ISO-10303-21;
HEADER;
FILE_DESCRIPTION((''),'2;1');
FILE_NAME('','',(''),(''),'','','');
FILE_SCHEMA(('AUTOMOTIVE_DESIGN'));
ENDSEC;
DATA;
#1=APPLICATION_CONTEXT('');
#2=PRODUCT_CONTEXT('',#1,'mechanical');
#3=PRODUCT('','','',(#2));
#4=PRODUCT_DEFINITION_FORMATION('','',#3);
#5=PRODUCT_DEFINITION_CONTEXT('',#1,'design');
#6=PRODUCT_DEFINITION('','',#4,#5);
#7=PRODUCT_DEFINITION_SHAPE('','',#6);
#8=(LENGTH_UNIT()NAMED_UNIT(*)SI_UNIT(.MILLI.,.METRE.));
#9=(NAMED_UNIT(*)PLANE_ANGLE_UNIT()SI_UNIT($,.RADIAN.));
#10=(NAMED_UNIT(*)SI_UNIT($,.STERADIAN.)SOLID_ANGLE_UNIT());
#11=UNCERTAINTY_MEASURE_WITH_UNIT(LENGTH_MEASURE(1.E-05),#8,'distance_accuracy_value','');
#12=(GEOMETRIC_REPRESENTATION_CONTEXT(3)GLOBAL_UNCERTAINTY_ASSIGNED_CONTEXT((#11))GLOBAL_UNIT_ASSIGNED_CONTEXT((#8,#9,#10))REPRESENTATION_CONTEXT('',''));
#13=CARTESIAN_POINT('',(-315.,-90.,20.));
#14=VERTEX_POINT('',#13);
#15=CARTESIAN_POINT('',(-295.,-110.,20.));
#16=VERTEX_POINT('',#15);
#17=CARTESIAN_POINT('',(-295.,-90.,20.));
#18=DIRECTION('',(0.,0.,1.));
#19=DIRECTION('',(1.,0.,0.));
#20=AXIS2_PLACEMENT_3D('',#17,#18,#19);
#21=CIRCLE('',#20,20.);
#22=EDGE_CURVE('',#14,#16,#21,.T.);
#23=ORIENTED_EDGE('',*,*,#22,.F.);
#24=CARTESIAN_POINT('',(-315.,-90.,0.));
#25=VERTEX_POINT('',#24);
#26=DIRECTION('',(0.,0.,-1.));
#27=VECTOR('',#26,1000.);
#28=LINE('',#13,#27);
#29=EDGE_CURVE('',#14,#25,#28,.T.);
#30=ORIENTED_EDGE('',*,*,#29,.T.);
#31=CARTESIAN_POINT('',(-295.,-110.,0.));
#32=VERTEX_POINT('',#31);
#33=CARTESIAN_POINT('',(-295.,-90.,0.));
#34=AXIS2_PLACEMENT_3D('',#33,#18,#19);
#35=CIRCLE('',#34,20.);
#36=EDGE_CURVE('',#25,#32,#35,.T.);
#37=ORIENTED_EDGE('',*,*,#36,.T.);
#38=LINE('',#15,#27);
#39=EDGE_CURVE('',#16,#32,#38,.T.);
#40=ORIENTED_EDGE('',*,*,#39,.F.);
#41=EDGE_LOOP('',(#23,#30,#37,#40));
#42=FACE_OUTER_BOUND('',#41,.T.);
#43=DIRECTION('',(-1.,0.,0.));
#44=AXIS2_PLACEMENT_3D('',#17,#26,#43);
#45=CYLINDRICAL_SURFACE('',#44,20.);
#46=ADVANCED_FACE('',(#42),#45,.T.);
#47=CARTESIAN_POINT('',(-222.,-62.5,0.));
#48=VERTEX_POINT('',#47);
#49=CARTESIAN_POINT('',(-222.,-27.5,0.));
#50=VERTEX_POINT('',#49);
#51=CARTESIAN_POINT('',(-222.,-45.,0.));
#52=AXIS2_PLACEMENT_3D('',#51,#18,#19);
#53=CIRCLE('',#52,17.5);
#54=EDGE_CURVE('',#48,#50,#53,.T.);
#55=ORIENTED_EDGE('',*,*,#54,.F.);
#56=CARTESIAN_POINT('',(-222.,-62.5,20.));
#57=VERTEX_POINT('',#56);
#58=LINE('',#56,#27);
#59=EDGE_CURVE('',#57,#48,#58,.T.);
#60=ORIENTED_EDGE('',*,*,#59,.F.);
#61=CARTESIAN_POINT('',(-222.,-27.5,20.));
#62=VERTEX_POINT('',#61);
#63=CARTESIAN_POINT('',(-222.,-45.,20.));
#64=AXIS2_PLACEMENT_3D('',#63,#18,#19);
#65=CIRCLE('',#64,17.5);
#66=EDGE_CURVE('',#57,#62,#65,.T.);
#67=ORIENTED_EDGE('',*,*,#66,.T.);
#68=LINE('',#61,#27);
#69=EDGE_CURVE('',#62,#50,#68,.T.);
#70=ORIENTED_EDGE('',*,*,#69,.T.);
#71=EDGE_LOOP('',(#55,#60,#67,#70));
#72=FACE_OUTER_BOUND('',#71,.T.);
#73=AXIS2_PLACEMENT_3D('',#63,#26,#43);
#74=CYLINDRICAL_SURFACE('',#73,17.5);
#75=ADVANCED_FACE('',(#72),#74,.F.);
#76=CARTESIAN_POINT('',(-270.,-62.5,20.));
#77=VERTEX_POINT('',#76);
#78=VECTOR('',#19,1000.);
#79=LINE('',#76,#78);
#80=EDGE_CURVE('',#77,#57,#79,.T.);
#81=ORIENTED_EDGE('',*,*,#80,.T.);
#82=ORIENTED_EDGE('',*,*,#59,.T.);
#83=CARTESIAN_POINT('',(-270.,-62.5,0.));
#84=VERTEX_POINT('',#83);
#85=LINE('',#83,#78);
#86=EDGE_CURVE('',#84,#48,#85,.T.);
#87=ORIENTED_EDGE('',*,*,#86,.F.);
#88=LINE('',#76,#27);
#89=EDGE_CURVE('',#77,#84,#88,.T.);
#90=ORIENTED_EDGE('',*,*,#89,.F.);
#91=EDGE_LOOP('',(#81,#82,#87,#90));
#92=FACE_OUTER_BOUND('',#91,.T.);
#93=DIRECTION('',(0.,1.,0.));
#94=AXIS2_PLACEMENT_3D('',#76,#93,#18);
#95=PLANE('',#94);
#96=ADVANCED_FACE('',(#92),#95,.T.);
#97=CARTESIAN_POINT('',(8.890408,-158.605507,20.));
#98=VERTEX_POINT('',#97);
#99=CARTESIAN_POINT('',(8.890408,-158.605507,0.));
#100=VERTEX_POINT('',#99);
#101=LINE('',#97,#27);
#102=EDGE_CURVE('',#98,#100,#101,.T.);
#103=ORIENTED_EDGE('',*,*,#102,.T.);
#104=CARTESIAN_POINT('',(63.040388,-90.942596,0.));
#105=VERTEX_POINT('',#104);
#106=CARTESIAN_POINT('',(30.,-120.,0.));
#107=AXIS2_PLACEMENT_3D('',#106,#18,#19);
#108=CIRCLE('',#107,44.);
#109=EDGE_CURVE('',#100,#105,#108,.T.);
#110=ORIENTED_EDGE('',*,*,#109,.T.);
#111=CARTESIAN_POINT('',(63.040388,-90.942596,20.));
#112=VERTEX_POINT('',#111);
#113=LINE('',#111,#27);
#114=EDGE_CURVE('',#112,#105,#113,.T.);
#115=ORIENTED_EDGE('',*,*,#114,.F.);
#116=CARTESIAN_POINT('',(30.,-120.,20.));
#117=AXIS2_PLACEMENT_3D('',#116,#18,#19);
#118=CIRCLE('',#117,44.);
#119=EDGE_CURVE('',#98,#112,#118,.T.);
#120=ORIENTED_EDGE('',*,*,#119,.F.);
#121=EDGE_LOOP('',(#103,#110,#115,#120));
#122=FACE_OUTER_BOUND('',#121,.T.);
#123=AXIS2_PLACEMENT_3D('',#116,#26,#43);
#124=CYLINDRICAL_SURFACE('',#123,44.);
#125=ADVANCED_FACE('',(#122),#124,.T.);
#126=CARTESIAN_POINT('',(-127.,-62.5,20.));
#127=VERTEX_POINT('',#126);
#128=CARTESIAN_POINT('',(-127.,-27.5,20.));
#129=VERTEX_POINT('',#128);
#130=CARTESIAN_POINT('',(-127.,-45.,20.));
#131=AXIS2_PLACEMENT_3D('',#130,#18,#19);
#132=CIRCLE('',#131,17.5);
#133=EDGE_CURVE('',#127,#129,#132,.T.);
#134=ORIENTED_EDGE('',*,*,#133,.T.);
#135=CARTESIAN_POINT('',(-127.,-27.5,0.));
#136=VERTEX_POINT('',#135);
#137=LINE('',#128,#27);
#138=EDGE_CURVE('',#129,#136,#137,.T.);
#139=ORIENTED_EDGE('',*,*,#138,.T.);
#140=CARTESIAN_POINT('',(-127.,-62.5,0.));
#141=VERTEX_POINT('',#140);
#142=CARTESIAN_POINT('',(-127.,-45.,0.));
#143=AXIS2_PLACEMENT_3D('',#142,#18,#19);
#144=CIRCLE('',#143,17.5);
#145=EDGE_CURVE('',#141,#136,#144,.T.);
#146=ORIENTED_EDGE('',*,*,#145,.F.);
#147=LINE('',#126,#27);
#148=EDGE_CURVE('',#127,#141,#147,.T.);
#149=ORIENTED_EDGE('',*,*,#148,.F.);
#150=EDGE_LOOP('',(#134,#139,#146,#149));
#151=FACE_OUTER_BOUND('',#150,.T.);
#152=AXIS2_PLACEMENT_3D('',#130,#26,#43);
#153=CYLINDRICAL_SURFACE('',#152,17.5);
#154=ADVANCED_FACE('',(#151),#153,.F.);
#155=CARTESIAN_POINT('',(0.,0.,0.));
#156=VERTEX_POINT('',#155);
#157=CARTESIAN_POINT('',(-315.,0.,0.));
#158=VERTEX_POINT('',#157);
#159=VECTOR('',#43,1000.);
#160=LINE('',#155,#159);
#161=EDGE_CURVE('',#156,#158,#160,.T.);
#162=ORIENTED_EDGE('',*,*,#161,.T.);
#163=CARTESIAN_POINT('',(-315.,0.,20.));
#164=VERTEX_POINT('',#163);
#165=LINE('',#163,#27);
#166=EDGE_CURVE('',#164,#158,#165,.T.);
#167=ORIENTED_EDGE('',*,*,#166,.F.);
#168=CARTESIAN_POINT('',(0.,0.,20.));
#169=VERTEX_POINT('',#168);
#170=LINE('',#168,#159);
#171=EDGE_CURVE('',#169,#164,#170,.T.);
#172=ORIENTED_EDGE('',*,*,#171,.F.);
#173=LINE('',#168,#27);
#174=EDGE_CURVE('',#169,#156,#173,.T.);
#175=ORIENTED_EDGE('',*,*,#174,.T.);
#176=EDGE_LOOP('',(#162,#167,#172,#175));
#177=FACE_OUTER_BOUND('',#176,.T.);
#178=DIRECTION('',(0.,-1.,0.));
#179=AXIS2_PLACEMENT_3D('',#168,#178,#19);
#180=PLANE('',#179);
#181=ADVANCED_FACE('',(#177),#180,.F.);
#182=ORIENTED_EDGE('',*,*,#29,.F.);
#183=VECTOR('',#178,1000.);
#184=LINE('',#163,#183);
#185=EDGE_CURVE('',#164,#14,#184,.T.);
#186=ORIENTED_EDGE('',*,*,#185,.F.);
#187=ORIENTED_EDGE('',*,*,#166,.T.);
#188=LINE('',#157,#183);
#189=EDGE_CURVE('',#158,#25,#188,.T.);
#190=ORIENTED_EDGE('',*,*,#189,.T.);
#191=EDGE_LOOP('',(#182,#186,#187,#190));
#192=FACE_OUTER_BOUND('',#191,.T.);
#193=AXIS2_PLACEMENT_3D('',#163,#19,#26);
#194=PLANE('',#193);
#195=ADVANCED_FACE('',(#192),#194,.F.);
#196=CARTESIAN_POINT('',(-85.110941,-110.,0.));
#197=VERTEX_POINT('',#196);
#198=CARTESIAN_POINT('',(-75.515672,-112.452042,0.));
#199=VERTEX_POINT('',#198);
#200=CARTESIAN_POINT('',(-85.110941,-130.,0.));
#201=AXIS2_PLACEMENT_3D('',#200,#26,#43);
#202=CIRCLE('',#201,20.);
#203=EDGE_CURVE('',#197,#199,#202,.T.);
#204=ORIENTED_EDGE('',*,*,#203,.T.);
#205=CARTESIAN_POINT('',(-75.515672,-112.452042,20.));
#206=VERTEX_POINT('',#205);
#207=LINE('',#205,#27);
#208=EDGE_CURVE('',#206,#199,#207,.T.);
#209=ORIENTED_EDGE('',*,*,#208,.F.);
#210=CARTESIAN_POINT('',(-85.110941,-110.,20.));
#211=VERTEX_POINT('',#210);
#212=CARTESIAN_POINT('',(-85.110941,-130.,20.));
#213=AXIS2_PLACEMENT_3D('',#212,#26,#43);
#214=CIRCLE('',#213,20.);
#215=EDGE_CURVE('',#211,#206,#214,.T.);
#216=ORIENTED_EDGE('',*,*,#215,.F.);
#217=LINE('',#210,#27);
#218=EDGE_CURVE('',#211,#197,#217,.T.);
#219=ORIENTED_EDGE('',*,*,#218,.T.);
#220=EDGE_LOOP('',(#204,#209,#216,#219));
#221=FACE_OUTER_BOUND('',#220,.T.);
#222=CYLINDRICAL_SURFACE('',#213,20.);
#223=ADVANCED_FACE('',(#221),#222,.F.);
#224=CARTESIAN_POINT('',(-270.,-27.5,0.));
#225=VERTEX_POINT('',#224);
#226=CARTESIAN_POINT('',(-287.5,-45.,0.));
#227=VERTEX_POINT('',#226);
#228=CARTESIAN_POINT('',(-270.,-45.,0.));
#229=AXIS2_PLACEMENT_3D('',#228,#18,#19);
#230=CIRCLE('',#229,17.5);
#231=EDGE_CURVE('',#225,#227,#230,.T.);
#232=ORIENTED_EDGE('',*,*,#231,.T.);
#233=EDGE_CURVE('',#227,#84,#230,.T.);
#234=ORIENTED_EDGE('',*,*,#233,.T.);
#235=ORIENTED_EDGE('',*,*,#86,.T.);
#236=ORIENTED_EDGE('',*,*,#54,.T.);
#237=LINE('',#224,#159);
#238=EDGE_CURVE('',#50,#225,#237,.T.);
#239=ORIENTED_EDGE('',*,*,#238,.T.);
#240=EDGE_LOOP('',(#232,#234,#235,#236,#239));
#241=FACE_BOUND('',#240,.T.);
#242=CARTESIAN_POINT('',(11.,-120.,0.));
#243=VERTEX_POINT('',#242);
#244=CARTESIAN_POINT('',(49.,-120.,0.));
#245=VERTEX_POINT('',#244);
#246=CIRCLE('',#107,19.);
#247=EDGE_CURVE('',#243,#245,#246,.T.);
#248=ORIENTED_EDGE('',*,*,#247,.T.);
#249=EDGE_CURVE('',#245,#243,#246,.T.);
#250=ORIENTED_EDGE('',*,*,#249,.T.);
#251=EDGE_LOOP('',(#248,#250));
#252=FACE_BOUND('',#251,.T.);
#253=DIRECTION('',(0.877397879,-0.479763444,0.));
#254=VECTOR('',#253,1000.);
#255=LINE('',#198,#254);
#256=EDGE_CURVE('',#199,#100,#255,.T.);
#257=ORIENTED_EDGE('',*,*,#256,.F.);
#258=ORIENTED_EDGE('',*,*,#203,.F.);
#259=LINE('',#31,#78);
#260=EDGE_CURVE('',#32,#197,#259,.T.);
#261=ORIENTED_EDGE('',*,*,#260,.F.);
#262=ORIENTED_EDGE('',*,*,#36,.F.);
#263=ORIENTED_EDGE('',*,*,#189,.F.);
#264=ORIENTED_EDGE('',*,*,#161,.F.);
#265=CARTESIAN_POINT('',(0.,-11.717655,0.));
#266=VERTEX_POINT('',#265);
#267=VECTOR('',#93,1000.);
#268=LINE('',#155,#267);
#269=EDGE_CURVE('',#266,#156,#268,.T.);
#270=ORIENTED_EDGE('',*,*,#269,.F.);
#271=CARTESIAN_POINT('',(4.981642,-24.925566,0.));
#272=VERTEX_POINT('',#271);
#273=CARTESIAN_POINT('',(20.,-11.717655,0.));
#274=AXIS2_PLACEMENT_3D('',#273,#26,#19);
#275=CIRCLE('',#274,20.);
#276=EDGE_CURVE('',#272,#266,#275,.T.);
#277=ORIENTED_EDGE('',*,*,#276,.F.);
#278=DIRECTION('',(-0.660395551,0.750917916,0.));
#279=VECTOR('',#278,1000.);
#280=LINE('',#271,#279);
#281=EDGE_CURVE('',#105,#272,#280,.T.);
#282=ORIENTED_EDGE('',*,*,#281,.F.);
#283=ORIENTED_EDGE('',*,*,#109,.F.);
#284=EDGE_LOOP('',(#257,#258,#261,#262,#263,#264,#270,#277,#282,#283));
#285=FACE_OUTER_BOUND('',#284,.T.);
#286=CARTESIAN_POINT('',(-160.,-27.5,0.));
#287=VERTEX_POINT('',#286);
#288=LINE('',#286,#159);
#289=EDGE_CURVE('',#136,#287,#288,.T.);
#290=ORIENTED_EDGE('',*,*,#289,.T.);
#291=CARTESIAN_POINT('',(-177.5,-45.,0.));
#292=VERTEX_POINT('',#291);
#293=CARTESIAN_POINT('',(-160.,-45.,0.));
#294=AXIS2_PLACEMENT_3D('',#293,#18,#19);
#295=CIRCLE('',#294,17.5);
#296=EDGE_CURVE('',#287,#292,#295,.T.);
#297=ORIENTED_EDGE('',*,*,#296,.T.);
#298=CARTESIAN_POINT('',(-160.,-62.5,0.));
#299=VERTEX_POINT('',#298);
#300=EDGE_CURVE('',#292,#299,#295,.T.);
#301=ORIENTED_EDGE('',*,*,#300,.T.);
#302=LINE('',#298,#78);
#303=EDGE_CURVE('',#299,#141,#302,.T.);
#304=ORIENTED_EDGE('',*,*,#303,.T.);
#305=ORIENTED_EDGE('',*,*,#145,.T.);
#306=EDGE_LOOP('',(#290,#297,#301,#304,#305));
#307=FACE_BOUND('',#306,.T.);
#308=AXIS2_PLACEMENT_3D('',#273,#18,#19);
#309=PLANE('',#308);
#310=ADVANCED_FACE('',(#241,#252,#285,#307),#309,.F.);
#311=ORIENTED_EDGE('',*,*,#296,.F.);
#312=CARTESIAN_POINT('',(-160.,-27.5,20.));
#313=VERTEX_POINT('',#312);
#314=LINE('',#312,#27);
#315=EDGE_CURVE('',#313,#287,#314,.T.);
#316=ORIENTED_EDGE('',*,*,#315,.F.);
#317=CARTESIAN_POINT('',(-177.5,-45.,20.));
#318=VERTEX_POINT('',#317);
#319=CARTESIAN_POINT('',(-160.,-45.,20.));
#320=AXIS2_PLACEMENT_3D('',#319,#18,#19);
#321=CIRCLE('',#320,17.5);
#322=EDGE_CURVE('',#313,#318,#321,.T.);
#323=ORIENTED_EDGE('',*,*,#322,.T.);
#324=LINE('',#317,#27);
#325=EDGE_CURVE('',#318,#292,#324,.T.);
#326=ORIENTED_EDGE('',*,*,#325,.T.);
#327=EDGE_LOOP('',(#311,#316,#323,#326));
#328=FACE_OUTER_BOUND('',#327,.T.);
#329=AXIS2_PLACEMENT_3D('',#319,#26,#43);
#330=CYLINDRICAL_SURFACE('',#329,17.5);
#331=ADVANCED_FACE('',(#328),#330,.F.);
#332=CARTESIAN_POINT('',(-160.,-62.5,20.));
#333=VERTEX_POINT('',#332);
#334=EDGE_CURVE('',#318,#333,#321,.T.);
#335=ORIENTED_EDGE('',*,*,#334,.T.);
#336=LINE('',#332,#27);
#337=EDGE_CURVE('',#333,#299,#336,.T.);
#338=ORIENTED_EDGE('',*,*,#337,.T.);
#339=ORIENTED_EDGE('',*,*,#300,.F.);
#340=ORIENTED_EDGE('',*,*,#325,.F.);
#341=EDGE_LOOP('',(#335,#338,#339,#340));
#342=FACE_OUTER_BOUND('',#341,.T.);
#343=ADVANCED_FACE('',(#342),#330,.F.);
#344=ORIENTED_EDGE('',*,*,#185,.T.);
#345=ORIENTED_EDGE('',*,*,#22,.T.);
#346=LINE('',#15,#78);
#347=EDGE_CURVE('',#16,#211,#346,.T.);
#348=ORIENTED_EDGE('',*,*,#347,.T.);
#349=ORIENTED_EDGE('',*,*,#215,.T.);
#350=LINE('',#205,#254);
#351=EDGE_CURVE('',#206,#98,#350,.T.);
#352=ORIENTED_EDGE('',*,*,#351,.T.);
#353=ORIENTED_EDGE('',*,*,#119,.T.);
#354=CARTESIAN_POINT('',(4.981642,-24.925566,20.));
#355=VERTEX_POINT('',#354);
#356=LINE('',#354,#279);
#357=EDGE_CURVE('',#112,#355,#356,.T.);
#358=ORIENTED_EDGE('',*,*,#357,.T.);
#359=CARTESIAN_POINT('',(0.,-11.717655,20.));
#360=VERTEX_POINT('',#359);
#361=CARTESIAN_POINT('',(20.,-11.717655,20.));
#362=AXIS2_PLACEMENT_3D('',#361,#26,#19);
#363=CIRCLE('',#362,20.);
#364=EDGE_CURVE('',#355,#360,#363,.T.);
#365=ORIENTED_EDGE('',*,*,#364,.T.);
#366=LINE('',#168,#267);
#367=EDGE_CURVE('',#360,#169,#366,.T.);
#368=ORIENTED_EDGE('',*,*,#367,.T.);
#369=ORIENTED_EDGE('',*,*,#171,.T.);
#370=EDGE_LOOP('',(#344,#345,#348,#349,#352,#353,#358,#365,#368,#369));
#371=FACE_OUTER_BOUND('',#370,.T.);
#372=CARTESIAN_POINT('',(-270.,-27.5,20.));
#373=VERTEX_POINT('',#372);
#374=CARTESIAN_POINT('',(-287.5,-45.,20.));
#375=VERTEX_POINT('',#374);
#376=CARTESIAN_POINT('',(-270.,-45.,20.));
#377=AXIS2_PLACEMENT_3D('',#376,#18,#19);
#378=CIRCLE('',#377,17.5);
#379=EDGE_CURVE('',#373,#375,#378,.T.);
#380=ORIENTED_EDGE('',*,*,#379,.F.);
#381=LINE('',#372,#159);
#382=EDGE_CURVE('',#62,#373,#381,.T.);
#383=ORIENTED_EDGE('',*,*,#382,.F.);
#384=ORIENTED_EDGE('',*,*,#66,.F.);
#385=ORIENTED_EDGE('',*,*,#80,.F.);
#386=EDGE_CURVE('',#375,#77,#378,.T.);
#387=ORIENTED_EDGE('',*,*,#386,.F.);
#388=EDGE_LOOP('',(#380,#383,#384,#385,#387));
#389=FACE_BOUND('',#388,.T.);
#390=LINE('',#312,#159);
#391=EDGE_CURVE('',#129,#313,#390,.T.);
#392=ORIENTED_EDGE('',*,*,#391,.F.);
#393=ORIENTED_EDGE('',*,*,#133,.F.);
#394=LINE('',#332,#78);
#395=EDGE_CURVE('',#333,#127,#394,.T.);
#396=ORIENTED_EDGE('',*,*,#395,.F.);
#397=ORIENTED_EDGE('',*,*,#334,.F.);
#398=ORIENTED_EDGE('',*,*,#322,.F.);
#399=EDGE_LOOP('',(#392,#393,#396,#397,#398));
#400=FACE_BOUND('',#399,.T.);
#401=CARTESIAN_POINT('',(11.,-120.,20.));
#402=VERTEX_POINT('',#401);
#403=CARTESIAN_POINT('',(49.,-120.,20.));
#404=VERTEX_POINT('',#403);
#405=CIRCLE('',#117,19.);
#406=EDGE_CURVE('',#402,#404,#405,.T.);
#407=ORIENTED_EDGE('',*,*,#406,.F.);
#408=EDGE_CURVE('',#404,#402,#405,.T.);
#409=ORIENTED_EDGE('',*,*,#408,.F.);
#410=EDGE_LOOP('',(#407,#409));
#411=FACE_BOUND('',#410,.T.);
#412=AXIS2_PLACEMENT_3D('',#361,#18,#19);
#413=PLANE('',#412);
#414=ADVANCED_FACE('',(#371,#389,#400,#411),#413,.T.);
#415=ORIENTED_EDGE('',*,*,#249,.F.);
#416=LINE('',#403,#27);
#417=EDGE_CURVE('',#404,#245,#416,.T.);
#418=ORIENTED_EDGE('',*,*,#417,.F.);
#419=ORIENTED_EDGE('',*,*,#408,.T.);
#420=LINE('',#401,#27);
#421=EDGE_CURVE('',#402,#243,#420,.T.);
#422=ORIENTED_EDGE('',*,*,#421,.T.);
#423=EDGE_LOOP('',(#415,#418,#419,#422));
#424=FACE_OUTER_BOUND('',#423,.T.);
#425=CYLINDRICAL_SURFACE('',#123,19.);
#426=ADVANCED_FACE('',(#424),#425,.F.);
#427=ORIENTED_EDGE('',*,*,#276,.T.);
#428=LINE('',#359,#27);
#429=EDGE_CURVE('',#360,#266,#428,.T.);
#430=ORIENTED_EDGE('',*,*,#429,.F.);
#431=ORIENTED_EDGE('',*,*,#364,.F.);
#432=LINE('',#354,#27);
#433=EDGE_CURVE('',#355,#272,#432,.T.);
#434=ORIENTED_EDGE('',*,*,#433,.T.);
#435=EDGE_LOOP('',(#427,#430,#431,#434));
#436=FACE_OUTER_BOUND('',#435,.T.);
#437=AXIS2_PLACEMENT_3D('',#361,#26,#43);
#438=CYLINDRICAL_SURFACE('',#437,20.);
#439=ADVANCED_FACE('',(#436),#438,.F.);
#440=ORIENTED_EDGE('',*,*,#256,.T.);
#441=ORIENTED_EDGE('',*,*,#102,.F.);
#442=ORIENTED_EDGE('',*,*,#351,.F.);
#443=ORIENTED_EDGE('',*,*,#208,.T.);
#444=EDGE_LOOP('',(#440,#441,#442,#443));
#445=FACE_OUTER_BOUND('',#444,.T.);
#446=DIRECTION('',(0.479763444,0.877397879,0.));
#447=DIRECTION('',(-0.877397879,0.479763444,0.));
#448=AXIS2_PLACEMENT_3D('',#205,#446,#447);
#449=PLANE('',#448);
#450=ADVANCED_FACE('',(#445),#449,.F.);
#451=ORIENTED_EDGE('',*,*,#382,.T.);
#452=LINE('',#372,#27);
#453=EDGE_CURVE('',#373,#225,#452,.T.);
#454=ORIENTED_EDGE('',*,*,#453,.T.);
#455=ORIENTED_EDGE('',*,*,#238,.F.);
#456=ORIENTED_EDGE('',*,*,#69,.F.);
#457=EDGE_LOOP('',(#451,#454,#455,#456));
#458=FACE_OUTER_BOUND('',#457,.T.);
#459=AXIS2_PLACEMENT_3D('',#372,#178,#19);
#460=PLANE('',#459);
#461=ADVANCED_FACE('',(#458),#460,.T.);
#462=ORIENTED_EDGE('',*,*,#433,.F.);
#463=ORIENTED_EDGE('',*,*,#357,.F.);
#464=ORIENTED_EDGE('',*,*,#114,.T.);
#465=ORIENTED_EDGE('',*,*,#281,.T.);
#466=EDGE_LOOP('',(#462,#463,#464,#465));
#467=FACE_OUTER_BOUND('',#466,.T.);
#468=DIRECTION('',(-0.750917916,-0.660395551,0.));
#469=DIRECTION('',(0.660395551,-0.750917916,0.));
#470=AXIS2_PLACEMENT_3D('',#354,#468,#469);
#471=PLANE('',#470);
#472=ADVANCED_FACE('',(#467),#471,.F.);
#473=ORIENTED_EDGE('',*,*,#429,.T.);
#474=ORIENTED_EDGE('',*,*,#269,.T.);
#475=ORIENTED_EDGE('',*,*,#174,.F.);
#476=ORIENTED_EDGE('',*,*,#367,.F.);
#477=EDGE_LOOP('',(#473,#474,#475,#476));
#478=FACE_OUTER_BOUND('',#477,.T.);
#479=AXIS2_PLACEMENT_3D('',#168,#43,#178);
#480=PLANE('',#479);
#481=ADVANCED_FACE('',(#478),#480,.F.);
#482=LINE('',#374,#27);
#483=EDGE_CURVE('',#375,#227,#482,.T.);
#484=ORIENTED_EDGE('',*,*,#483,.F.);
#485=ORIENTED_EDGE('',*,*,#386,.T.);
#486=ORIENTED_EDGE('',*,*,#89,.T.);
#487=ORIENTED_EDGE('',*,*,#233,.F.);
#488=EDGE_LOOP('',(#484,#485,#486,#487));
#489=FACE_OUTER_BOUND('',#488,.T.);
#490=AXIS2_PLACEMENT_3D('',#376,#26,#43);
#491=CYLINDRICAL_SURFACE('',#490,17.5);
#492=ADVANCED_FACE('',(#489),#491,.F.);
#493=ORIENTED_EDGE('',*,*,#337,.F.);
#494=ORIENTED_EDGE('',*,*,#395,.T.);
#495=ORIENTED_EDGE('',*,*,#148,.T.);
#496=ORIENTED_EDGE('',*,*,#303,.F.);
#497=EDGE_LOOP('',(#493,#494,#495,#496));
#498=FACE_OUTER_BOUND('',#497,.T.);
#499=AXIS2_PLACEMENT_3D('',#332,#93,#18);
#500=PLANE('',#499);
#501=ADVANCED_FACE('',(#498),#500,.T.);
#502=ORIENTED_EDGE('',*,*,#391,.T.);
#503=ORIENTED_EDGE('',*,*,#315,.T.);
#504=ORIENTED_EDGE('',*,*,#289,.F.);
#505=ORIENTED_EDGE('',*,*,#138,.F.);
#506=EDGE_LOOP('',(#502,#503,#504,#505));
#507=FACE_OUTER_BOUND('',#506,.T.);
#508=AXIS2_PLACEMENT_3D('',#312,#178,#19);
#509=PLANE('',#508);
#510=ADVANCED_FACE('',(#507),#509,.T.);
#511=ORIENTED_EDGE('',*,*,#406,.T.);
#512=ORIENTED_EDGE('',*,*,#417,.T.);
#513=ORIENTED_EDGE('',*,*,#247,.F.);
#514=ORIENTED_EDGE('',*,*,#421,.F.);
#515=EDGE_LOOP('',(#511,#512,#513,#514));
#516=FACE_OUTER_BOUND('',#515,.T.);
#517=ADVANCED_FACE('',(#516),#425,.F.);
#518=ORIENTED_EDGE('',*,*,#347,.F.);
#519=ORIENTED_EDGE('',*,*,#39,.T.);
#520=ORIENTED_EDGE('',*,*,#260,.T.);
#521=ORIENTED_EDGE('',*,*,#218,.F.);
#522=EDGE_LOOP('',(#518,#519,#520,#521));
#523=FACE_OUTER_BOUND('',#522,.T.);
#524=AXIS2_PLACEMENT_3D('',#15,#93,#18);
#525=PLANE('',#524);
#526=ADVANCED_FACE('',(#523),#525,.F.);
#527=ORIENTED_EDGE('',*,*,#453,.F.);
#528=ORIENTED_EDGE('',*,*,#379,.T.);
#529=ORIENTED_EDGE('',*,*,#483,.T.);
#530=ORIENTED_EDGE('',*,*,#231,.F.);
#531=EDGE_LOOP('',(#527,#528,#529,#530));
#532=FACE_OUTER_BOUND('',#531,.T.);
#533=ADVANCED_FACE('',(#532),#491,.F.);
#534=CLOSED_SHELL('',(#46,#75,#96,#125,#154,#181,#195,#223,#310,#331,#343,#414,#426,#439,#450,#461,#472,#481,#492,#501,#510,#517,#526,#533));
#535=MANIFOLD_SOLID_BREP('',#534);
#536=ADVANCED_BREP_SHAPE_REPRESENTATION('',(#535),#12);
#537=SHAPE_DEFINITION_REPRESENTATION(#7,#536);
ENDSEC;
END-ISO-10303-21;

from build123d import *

# Parameters (mm, degrees)
SKETCH_3_R      = 19
EXTRUDE_2_DEPTH = 20


with BuildPart() as part:
    # 草图3 → 凸台-拉伸2 (new body)
    with BuildSketch(Plane.XY):
        with BuildLine():
            Line((0, 0), (-315, 0))
            Line((-315, 0), (-315, -90))
            ThreePointArc((-315, -90), (-309.142135624, -104.142135624), (-295, -110))
            Line((-295, -110), (-85.110940509, -110))
            ThreePointArc((-85.110940509, -110), (-80.159130316, -110.622704631), (-75.515671638, -112.452042418))
            Line((-75.515671638, -112.452042418), (8.890408484, -158.60550668))
            ThreePointArc((8.890408484, -158.60550668), (64.353360189, -147.492665271), (63.040388304, -90.942595767))
            Line((63.040388304, -90.942595767), (4.98164168, -24.925565564))
            ThreePointArc((4.98164168, -24.925565564), (1.286807242, -18.775729131), (0, -11.71765455))
            Line((0, -11.71765455), (0, 0))
        make_face()
        with Locations((30, -120)):
            Circle(SKETCH_3_R, mode=Mode.SUBTRACT)
        with BuildLine():
            Line((-270, -27.5), (-222, -27.5))
            ThreePointArc((-222, -27.5), (-204.5, -45), (-222, -62.5))
            Line((-222, -62.5), (-270, -62.5))
            ThreePointArc((-270, -62.5), (-287.5, -45), (-270, -27.5))
        make_face(mode=Mode.SUBTRACT)
        with BuildLine():
            Line((-160, -27.5), (-127, -27.5))
            ThreePointArc((-127, -27.5), (-109.5, -45), (-127, -62.5))
            Line((-127, -62.5), (-160, -62.5))
            ThreePointArc((-160, -62.5), (-177.5, -45), (-160, -27.5))
        make_face(mode=Mode.SUBTRACT)
    extrude(amount=EXTRUDE_2_DEPTH)


solid = part.part
